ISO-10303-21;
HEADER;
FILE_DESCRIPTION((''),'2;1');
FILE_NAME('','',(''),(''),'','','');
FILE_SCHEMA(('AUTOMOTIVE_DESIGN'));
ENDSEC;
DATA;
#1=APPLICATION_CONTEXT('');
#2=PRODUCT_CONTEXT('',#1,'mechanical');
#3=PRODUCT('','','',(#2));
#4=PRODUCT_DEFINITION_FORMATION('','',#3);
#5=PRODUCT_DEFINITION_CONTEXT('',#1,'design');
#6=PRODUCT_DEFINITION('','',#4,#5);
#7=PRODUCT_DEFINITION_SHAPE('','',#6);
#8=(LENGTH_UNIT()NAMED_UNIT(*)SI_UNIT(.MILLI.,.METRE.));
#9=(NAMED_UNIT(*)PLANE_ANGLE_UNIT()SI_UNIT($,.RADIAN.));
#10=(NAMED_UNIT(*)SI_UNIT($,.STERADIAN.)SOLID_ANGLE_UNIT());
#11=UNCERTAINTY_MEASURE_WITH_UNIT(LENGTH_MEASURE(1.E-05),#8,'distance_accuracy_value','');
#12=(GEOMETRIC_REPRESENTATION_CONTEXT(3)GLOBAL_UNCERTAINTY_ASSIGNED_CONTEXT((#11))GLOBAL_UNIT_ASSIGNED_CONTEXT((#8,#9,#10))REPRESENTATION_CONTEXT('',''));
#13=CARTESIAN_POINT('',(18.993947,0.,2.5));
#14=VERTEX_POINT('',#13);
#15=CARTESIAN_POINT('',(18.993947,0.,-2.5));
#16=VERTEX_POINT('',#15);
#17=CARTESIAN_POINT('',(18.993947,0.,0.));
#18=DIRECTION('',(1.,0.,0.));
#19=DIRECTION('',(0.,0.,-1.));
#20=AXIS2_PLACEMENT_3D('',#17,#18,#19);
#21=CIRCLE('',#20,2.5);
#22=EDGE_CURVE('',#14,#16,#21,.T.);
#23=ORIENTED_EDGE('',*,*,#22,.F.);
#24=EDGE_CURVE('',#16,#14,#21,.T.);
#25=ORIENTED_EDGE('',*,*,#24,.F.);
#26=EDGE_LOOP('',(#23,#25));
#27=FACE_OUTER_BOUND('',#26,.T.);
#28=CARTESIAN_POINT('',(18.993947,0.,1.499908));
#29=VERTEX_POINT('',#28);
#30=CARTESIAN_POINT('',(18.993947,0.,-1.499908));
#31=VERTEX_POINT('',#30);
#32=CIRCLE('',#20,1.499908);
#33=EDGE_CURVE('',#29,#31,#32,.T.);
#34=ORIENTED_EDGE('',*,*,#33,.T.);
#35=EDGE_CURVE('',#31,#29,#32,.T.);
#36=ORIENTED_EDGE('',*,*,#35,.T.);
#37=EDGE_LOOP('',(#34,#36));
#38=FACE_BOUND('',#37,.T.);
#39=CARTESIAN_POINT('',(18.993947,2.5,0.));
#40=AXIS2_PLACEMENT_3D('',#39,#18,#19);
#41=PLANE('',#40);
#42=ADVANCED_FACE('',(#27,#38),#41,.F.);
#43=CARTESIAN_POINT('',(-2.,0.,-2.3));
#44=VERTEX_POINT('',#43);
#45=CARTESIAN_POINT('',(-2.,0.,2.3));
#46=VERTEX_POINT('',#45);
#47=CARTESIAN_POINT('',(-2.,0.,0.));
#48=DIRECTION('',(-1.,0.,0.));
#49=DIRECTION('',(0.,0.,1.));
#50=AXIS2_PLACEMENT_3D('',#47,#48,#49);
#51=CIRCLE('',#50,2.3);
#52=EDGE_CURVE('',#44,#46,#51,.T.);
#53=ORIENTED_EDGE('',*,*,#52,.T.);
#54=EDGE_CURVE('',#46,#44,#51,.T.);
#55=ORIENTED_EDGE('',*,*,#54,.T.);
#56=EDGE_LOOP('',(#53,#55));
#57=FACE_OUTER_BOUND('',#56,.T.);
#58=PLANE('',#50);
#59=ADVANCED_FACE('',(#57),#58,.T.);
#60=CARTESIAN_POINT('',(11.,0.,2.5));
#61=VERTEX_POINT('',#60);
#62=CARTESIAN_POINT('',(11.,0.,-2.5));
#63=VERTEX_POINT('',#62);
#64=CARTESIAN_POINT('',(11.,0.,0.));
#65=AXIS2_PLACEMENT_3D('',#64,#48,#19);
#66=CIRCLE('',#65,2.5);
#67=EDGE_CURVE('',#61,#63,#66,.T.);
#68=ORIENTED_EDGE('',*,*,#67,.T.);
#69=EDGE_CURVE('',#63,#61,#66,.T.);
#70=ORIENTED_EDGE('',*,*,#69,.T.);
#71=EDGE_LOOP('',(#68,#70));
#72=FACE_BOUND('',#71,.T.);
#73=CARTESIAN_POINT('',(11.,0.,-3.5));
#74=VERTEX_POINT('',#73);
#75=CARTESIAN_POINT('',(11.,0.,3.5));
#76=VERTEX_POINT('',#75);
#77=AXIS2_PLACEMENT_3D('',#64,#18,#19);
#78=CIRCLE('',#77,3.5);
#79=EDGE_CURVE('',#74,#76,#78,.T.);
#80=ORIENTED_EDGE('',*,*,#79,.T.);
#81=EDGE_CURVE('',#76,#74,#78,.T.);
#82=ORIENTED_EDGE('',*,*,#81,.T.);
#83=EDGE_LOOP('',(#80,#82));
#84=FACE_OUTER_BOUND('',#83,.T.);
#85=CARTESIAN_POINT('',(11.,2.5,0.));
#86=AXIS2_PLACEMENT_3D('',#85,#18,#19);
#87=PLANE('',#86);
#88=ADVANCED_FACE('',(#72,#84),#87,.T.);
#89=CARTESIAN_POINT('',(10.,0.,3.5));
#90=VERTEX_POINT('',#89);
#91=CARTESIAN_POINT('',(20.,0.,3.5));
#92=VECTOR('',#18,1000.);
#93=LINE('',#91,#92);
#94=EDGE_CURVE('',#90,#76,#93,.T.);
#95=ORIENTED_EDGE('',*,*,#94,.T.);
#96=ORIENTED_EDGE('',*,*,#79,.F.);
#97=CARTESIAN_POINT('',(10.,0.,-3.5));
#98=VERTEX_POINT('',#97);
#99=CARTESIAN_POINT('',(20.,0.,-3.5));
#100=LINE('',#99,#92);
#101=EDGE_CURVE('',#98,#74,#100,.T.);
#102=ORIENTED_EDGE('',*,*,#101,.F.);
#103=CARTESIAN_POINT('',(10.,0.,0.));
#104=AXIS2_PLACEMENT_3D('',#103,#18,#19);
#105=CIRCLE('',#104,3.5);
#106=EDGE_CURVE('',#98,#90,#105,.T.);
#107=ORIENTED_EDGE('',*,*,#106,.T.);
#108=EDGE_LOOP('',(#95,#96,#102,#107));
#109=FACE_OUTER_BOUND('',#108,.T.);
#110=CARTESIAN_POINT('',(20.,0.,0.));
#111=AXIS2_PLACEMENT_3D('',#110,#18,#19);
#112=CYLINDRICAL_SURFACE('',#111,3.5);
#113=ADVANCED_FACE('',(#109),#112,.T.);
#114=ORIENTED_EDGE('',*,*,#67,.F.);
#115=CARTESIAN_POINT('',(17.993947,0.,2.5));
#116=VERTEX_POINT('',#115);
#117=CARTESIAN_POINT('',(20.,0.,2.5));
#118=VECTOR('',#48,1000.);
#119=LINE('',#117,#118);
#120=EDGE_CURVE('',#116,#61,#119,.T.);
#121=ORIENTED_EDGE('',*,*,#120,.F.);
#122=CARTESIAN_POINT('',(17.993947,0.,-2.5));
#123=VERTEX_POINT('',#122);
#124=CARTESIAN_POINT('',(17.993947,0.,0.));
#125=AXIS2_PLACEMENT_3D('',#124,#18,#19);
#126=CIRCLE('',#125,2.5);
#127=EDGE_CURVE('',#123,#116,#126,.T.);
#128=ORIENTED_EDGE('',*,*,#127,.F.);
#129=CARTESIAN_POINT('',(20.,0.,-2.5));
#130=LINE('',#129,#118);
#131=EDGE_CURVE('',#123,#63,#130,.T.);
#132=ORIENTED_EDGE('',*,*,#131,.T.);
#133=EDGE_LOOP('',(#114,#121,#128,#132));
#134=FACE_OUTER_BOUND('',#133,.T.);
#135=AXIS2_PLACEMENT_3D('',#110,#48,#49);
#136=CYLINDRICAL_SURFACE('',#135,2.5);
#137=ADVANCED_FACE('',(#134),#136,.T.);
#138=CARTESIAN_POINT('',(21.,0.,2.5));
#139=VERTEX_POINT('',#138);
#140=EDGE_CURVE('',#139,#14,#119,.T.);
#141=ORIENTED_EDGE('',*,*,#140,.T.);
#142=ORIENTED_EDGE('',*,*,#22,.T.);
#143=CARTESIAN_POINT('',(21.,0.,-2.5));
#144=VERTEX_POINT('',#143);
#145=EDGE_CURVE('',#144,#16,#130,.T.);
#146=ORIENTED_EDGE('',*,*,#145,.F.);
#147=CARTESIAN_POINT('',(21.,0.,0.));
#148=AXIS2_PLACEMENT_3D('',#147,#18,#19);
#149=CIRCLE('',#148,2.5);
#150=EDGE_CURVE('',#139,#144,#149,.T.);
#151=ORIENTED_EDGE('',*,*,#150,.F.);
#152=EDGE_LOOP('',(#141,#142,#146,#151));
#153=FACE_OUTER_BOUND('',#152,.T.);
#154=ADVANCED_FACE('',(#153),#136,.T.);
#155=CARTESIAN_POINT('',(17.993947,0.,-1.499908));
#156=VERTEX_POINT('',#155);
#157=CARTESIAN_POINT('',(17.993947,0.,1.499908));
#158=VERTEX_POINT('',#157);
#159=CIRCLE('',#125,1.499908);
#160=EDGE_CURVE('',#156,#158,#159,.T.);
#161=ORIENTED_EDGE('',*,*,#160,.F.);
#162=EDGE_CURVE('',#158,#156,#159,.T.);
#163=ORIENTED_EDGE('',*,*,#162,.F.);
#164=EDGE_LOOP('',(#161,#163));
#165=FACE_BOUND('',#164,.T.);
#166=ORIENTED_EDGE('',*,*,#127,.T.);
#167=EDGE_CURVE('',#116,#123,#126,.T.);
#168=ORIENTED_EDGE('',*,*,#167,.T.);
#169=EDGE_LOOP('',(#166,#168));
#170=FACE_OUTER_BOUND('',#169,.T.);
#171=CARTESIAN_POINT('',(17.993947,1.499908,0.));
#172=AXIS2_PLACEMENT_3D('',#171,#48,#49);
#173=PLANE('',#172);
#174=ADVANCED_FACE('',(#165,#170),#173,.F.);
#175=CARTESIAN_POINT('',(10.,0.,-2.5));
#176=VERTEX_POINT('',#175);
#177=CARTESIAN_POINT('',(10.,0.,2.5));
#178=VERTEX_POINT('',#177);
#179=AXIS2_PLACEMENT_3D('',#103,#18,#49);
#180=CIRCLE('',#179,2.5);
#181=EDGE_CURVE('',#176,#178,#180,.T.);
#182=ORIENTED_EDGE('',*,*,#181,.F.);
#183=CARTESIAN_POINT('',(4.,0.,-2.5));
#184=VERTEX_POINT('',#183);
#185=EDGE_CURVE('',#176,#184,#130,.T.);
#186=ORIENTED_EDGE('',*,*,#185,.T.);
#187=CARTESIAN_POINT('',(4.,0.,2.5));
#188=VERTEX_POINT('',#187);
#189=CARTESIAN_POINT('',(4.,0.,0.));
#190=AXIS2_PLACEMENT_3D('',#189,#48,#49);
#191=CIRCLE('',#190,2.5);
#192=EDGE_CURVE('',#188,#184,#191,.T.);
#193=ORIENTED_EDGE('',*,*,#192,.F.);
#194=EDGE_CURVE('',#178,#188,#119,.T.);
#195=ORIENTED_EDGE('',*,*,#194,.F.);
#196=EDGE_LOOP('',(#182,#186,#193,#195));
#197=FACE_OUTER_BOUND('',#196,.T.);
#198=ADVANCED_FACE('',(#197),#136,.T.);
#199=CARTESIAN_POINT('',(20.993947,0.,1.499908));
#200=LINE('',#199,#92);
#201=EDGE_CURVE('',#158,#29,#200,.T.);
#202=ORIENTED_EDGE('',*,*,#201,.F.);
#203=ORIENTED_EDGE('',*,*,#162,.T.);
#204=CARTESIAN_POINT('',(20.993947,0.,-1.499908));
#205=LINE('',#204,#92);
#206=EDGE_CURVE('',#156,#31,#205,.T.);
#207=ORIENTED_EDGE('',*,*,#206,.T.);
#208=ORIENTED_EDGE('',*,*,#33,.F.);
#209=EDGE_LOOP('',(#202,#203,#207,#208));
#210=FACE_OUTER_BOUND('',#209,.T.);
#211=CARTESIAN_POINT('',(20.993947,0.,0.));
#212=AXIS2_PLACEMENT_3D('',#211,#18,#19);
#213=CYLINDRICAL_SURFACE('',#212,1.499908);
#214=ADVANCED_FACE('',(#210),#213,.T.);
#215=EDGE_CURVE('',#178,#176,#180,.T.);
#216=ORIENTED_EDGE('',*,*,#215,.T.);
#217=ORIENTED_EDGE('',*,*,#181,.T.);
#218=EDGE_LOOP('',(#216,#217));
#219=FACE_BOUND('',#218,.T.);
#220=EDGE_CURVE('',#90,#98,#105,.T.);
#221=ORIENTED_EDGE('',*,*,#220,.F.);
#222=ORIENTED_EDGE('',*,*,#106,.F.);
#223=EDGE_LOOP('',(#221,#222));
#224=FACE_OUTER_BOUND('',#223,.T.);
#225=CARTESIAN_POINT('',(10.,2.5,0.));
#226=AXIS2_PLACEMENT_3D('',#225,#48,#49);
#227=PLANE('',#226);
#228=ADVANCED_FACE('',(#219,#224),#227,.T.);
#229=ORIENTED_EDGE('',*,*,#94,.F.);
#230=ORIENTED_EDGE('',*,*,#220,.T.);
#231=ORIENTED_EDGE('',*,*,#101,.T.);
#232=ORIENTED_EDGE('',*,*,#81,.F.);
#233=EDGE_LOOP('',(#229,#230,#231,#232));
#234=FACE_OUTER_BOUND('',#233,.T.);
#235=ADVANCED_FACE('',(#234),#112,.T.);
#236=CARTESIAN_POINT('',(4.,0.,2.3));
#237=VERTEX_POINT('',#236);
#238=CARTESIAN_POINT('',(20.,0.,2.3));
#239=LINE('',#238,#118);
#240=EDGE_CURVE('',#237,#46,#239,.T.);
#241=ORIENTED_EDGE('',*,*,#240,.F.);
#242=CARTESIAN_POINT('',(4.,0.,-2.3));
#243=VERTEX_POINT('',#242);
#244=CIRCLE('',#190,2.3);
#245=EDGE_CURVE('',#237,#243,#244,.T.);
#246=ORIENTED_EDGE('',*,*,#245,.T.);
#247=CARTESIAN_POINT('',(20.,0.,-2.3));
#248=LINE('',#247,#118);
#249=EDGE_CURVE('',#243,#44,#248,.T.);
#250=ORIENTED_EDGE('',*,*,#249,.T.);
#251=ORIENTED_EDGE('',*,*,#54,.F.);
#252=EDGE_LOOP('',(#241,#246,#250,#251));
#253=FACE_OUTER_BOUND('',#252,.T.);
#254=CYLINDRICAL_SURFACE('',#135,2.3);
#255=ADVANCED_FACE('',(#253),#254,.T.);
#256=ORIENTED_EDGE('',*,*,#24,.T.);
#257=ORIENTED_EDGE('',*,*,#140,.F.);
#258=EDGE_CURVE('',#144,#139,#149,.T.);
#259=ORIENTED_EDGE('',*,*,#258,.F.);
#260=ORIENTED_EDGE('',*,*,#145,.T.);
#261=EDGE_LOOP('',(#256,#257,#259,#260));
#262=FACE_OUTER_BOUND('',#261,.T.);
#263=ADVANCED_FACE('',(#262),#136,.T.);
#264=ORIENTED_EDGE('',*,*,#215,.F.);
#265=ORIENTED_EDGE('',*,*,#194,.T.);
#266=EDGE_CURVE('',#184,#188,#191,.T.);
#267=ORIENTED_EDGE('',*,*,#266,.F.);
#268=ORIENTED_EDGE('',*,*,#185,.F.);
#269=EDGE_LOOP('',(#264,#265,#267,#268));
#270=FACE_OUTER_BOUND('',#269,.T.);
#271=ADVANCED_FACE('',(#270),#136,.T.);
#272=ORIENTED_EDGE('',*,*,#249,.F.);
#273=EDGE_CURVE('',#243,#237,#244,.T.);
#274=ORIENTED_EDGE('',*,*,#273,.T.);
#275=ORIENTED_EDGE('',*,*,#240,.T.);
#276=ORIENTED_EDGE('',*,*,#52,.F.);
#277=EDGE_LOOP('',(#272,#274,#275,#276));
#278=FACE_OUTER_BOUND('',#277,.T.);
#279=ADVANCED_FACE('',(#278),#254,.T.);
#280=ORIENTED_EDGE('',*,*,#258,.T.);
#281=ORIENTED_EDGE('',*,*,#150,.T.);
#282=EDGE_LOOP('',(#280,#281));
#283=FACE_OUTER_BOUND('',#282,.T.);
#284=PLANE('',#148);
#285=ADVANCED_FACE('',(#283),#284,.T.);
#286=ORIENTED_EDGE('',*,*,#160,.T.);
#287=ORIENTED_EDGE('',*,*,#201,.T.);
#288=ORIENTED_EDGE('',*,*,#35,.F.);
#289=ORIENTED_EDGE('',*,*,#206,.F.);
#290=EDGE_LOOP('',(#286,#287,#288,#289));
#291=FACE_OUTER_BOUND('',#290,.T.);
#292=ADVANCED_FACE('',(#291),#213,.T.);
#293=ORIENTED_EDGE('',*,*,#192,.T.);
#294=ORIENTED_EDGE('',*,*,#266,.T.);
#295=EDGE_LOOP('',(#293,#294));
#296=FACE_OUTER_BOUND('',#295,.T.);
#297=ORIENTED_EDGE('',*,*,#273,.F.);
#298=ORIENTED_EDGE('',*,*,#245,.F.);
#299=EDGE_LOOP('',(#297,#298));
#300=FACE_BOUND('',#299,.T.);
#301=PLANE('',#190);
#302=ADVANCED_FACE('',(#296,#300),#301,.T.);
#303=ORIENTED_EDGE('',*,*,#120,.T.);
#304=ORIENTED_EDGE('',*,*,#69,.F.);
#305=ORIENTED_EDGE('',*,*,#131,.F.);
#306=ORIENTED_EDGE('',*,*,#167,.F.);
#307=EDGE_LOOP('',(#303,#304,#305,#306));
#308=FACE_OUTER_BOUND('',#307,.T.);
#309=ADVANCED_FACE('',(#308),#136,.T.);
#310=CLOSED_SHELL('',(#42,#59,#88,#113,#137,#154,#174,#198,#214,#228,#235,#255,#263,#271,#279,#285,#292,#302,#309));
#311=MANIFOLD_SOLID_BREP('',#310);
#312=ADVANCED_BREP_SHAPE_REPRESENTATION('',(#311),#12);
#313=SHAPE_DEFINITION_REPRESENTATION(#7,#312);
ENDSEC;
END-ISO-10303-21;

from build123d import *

# Parameters (mm, degrees)
SKETCH1_R           = 2.3
BOSS_EXTRUDE1_DEPTH = 20
SKETCH3_W           = 0.694541754
SKETCH3_H           = 0.2
BOSS_EXTRUDE2_START = 2
SKETCH4_R           = 2.3
BOSS_EXTRUDE2_DEPTH = 2
SKETCH5_R           = 2.5
BOSS_EXTRUDE3_DEPTH = 10
SKETCH6_W           = 1
SKETCH6_H           = 1.000091558
SKETCH10_R          = 2.5
BOSS_EXTRUDE4_DEPTH = 6
SKETCH11_W          = 1
SKETCH11_H          = 1
BOSS_EXTRUDE5_START = 1
SKETCH12_R          = 2.5
BOSS_EXTRUDE5_DEPTH = 1


with BuildPart() as part:
    # Sketch1 → Boss-Extrude1 (new body)
    with BuildSketch(Plane(origin=(0, 0, 0), x_dir=(0, 0, -1), z_dir=(1, 0, 0))):
        Circle(SKETCH1_R)
    extrude(amount=BOSS_EXTRUDE1_DEPTH)

    # Sketch3 → Revolve1 (revolve)
    with BuildSketch(Plane.XY, mode=Mode.PRIVATE) as revolve1_sk:
        with Locations((10.347270877, 2.4)):
            Rectangle(SKETCH3_W, SKETCH3_H)
    revolve(revolve1_sk.sketch.rotate(Axis((20, 0, 0), (-1, 0, 0)), 270), axis=Axis((20, 0, 0), (-1, 0, 0)))

    # Sketch4 → Boss-Extrude2 (add)
    with BuildSketch(Plane.ZY.offset(BOSS_EXTRUDE2_START)):
        Circle(SKETCH4_R)
    extrude(amount=-BOSS_EXTRUDE2_DEPTH)

    # Sketch5 → Boss-Extrude3 (add)
    with BuildSketch(Plane(origin=(20, 0, 0), x_dir=(0, 0, -1), z_dir=(1, 0, 0))):
        with Locations(Location((0, 0, 0), (0, 0, 180))):
            Circle(SKETCH5_R)
    extrude(amount=-BOSS_EXTRUDE3_DEPTH)

    # Sketch6 → Cut-Revolve1 (revolve, cut)
    with BuildSketch(Plane(origin=(0.993947206, 0, 0), x_dir=(1, 0, 0), z_dir=(0, 0, 1)), mode=Mode.PRIVATE) as cut_revolve1_sk:
        with Locations((17.5, 1.999954221)):
            Rectangle(SKETCH6_W, SKETCH6_H)
    revolve(cut_revolve1_sk.sketch.rotate(Axis((20.993947206, 0, 0), (-1, 0, 0)), 270), axis=Axis((20.993947206, 0, 0), (-1, 0, 0)), mode=Mode.SUBTRACT)

    # Sketch10 → Boss-Extrude4 (add)
    with BuildSketch(Plane.ZY.offset(-10)):
        Circle(SKETCH10_R)
    extrude(amount=BOSS_EXTRUDE4_DEPTH)

    # Sketch11 → Revolve2 (revolve)
    with BuildSketch(Plane.XY, mode=Mode.PRIVATE) as revolve2_sk:
        with Locations((10.5, 3)):
            Rectangle(SKETCH11_W, SKETCH11_H)
    revolve(revolve2_sk.sketch.rotate(Axis((20, 0, 0), (-1, 0, 0)), 90), axis=Axis((20, 0, 0), (-1, 0, 0)))

    # Sketch12 → Boss-Extrude5 (add)
    with BuildSketch(Plane(origin=(20, 0, 0), x_dir=(0, 0, -1), z_dir=(1, 0, 0)).offset(BOSS_EXTRUDE5_START)):
        Circle(SKETCH12_R)
    extrude(amount=-BOSS_EXTRUDE5_DEPTH)


solid = part.part
